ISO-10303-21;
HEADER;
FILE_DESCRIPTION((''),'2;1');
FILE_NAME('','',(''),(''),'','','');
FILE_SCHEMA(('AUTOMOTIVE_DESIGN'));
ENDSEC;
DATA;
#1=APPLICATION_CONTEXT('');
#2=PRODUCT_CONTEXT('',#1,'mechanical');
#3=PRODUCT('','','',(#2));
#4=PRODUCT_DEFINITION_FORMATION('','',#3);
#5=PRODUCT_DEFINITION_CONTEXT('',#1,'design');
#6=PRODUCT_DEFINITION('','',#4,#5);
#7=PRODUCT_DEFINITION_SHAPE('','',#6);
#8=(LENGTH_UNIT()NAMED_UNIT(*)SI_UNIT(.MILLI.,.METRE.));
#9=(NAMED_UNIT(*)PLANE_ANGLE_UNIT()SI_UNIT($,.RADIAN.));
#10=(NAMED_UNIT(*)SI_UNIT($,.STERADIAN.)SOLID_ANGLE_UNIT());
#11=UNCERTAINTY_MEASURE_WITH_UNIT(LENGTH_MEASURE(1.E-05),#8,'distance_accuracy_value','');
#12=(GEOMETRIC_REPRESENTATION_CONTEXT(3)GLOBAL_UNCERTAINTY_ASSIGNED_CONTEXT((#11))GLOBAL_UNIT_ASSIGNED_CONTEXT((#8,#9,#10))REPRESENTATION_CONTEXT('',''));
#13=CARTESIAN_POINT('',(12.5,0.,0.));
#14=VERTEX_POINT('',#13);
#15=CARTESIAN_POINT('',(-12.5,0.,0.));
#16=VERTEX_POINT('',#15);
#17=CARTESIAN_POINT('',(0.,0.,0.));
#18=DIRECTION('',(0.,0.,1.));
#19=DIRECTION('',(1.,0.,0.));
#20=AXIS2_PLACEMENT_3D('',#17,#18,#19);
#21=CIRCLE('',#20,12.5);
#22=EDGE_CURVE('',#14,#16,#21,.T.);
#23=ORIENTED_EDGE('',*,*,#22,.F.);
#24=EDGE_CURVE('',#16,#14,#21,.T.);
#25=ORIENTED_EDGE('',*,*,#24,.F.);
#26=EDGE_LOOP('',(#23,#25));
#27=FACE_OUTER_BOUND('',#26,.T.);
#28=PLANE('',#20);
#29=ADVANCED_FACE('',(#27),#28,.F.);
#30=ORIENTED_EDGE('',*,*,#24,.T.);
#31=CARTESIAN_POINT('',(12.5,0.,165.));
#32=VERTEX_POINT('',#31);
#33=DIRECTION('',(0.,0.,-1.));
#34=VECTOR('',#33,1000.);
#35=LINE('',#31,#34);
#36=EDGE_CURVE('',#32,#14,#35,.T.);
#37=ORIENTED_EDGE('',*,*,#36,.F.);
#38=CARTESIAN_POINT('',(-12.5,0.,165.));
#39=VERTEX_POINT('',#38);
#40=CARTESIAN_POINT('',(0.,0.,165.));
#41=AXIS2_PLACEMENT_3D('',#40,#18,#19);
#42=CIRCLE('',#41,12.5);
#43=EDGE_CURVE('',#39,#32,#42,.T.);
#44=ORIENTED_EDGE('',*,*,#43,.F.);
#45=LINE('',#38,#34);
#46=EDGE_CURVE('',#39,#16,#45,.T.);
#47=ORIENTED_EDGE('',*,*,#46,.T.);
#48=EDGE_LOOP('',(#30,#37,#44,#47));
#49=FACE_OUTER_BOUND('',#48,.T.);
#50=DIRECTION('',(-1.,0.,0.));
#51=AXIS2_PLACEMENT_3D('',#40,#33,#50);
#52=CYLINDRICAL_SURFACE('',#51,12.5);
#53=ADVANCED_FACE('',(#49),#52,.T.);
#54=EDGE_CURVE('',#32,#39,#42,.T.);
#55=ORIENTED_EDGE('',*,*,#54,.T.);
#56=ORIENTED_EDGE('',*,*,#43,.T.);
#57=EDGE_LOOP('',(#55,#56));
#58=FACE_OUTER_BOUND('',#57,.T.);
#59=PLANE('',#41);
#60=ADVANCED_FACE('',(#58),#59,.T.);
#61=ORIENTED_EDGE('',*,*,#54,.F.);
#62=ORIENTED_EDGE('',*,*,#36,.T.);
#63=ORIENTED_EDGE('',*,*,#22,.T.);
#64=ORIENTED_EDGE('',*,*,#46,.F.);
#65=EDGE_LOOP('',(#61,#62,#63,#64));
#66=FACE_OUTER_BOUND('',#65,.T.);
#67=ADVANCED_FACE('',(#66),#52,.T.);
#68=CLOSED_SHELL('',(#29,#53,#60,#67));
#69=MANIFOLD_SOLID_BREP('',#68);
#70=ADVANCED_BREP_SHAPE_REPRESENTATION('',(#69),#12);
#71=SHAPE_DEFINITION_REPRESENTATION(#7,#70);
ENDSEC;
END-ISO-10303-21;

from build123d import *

# Parameters (mm, degrees)
SKETCH_1_R      = 12.5
EXTRUDE_1_DEPTH = 165


with BuildPart() as part:
    # 草图1 → 凸台-拉伸1 (new body)
    with BuildSketch(Plane.XY):
        Circle(SKETCH_1_R)
    extrude(amount=EXTRUDE_1_DEPTH)


solid = part.part
